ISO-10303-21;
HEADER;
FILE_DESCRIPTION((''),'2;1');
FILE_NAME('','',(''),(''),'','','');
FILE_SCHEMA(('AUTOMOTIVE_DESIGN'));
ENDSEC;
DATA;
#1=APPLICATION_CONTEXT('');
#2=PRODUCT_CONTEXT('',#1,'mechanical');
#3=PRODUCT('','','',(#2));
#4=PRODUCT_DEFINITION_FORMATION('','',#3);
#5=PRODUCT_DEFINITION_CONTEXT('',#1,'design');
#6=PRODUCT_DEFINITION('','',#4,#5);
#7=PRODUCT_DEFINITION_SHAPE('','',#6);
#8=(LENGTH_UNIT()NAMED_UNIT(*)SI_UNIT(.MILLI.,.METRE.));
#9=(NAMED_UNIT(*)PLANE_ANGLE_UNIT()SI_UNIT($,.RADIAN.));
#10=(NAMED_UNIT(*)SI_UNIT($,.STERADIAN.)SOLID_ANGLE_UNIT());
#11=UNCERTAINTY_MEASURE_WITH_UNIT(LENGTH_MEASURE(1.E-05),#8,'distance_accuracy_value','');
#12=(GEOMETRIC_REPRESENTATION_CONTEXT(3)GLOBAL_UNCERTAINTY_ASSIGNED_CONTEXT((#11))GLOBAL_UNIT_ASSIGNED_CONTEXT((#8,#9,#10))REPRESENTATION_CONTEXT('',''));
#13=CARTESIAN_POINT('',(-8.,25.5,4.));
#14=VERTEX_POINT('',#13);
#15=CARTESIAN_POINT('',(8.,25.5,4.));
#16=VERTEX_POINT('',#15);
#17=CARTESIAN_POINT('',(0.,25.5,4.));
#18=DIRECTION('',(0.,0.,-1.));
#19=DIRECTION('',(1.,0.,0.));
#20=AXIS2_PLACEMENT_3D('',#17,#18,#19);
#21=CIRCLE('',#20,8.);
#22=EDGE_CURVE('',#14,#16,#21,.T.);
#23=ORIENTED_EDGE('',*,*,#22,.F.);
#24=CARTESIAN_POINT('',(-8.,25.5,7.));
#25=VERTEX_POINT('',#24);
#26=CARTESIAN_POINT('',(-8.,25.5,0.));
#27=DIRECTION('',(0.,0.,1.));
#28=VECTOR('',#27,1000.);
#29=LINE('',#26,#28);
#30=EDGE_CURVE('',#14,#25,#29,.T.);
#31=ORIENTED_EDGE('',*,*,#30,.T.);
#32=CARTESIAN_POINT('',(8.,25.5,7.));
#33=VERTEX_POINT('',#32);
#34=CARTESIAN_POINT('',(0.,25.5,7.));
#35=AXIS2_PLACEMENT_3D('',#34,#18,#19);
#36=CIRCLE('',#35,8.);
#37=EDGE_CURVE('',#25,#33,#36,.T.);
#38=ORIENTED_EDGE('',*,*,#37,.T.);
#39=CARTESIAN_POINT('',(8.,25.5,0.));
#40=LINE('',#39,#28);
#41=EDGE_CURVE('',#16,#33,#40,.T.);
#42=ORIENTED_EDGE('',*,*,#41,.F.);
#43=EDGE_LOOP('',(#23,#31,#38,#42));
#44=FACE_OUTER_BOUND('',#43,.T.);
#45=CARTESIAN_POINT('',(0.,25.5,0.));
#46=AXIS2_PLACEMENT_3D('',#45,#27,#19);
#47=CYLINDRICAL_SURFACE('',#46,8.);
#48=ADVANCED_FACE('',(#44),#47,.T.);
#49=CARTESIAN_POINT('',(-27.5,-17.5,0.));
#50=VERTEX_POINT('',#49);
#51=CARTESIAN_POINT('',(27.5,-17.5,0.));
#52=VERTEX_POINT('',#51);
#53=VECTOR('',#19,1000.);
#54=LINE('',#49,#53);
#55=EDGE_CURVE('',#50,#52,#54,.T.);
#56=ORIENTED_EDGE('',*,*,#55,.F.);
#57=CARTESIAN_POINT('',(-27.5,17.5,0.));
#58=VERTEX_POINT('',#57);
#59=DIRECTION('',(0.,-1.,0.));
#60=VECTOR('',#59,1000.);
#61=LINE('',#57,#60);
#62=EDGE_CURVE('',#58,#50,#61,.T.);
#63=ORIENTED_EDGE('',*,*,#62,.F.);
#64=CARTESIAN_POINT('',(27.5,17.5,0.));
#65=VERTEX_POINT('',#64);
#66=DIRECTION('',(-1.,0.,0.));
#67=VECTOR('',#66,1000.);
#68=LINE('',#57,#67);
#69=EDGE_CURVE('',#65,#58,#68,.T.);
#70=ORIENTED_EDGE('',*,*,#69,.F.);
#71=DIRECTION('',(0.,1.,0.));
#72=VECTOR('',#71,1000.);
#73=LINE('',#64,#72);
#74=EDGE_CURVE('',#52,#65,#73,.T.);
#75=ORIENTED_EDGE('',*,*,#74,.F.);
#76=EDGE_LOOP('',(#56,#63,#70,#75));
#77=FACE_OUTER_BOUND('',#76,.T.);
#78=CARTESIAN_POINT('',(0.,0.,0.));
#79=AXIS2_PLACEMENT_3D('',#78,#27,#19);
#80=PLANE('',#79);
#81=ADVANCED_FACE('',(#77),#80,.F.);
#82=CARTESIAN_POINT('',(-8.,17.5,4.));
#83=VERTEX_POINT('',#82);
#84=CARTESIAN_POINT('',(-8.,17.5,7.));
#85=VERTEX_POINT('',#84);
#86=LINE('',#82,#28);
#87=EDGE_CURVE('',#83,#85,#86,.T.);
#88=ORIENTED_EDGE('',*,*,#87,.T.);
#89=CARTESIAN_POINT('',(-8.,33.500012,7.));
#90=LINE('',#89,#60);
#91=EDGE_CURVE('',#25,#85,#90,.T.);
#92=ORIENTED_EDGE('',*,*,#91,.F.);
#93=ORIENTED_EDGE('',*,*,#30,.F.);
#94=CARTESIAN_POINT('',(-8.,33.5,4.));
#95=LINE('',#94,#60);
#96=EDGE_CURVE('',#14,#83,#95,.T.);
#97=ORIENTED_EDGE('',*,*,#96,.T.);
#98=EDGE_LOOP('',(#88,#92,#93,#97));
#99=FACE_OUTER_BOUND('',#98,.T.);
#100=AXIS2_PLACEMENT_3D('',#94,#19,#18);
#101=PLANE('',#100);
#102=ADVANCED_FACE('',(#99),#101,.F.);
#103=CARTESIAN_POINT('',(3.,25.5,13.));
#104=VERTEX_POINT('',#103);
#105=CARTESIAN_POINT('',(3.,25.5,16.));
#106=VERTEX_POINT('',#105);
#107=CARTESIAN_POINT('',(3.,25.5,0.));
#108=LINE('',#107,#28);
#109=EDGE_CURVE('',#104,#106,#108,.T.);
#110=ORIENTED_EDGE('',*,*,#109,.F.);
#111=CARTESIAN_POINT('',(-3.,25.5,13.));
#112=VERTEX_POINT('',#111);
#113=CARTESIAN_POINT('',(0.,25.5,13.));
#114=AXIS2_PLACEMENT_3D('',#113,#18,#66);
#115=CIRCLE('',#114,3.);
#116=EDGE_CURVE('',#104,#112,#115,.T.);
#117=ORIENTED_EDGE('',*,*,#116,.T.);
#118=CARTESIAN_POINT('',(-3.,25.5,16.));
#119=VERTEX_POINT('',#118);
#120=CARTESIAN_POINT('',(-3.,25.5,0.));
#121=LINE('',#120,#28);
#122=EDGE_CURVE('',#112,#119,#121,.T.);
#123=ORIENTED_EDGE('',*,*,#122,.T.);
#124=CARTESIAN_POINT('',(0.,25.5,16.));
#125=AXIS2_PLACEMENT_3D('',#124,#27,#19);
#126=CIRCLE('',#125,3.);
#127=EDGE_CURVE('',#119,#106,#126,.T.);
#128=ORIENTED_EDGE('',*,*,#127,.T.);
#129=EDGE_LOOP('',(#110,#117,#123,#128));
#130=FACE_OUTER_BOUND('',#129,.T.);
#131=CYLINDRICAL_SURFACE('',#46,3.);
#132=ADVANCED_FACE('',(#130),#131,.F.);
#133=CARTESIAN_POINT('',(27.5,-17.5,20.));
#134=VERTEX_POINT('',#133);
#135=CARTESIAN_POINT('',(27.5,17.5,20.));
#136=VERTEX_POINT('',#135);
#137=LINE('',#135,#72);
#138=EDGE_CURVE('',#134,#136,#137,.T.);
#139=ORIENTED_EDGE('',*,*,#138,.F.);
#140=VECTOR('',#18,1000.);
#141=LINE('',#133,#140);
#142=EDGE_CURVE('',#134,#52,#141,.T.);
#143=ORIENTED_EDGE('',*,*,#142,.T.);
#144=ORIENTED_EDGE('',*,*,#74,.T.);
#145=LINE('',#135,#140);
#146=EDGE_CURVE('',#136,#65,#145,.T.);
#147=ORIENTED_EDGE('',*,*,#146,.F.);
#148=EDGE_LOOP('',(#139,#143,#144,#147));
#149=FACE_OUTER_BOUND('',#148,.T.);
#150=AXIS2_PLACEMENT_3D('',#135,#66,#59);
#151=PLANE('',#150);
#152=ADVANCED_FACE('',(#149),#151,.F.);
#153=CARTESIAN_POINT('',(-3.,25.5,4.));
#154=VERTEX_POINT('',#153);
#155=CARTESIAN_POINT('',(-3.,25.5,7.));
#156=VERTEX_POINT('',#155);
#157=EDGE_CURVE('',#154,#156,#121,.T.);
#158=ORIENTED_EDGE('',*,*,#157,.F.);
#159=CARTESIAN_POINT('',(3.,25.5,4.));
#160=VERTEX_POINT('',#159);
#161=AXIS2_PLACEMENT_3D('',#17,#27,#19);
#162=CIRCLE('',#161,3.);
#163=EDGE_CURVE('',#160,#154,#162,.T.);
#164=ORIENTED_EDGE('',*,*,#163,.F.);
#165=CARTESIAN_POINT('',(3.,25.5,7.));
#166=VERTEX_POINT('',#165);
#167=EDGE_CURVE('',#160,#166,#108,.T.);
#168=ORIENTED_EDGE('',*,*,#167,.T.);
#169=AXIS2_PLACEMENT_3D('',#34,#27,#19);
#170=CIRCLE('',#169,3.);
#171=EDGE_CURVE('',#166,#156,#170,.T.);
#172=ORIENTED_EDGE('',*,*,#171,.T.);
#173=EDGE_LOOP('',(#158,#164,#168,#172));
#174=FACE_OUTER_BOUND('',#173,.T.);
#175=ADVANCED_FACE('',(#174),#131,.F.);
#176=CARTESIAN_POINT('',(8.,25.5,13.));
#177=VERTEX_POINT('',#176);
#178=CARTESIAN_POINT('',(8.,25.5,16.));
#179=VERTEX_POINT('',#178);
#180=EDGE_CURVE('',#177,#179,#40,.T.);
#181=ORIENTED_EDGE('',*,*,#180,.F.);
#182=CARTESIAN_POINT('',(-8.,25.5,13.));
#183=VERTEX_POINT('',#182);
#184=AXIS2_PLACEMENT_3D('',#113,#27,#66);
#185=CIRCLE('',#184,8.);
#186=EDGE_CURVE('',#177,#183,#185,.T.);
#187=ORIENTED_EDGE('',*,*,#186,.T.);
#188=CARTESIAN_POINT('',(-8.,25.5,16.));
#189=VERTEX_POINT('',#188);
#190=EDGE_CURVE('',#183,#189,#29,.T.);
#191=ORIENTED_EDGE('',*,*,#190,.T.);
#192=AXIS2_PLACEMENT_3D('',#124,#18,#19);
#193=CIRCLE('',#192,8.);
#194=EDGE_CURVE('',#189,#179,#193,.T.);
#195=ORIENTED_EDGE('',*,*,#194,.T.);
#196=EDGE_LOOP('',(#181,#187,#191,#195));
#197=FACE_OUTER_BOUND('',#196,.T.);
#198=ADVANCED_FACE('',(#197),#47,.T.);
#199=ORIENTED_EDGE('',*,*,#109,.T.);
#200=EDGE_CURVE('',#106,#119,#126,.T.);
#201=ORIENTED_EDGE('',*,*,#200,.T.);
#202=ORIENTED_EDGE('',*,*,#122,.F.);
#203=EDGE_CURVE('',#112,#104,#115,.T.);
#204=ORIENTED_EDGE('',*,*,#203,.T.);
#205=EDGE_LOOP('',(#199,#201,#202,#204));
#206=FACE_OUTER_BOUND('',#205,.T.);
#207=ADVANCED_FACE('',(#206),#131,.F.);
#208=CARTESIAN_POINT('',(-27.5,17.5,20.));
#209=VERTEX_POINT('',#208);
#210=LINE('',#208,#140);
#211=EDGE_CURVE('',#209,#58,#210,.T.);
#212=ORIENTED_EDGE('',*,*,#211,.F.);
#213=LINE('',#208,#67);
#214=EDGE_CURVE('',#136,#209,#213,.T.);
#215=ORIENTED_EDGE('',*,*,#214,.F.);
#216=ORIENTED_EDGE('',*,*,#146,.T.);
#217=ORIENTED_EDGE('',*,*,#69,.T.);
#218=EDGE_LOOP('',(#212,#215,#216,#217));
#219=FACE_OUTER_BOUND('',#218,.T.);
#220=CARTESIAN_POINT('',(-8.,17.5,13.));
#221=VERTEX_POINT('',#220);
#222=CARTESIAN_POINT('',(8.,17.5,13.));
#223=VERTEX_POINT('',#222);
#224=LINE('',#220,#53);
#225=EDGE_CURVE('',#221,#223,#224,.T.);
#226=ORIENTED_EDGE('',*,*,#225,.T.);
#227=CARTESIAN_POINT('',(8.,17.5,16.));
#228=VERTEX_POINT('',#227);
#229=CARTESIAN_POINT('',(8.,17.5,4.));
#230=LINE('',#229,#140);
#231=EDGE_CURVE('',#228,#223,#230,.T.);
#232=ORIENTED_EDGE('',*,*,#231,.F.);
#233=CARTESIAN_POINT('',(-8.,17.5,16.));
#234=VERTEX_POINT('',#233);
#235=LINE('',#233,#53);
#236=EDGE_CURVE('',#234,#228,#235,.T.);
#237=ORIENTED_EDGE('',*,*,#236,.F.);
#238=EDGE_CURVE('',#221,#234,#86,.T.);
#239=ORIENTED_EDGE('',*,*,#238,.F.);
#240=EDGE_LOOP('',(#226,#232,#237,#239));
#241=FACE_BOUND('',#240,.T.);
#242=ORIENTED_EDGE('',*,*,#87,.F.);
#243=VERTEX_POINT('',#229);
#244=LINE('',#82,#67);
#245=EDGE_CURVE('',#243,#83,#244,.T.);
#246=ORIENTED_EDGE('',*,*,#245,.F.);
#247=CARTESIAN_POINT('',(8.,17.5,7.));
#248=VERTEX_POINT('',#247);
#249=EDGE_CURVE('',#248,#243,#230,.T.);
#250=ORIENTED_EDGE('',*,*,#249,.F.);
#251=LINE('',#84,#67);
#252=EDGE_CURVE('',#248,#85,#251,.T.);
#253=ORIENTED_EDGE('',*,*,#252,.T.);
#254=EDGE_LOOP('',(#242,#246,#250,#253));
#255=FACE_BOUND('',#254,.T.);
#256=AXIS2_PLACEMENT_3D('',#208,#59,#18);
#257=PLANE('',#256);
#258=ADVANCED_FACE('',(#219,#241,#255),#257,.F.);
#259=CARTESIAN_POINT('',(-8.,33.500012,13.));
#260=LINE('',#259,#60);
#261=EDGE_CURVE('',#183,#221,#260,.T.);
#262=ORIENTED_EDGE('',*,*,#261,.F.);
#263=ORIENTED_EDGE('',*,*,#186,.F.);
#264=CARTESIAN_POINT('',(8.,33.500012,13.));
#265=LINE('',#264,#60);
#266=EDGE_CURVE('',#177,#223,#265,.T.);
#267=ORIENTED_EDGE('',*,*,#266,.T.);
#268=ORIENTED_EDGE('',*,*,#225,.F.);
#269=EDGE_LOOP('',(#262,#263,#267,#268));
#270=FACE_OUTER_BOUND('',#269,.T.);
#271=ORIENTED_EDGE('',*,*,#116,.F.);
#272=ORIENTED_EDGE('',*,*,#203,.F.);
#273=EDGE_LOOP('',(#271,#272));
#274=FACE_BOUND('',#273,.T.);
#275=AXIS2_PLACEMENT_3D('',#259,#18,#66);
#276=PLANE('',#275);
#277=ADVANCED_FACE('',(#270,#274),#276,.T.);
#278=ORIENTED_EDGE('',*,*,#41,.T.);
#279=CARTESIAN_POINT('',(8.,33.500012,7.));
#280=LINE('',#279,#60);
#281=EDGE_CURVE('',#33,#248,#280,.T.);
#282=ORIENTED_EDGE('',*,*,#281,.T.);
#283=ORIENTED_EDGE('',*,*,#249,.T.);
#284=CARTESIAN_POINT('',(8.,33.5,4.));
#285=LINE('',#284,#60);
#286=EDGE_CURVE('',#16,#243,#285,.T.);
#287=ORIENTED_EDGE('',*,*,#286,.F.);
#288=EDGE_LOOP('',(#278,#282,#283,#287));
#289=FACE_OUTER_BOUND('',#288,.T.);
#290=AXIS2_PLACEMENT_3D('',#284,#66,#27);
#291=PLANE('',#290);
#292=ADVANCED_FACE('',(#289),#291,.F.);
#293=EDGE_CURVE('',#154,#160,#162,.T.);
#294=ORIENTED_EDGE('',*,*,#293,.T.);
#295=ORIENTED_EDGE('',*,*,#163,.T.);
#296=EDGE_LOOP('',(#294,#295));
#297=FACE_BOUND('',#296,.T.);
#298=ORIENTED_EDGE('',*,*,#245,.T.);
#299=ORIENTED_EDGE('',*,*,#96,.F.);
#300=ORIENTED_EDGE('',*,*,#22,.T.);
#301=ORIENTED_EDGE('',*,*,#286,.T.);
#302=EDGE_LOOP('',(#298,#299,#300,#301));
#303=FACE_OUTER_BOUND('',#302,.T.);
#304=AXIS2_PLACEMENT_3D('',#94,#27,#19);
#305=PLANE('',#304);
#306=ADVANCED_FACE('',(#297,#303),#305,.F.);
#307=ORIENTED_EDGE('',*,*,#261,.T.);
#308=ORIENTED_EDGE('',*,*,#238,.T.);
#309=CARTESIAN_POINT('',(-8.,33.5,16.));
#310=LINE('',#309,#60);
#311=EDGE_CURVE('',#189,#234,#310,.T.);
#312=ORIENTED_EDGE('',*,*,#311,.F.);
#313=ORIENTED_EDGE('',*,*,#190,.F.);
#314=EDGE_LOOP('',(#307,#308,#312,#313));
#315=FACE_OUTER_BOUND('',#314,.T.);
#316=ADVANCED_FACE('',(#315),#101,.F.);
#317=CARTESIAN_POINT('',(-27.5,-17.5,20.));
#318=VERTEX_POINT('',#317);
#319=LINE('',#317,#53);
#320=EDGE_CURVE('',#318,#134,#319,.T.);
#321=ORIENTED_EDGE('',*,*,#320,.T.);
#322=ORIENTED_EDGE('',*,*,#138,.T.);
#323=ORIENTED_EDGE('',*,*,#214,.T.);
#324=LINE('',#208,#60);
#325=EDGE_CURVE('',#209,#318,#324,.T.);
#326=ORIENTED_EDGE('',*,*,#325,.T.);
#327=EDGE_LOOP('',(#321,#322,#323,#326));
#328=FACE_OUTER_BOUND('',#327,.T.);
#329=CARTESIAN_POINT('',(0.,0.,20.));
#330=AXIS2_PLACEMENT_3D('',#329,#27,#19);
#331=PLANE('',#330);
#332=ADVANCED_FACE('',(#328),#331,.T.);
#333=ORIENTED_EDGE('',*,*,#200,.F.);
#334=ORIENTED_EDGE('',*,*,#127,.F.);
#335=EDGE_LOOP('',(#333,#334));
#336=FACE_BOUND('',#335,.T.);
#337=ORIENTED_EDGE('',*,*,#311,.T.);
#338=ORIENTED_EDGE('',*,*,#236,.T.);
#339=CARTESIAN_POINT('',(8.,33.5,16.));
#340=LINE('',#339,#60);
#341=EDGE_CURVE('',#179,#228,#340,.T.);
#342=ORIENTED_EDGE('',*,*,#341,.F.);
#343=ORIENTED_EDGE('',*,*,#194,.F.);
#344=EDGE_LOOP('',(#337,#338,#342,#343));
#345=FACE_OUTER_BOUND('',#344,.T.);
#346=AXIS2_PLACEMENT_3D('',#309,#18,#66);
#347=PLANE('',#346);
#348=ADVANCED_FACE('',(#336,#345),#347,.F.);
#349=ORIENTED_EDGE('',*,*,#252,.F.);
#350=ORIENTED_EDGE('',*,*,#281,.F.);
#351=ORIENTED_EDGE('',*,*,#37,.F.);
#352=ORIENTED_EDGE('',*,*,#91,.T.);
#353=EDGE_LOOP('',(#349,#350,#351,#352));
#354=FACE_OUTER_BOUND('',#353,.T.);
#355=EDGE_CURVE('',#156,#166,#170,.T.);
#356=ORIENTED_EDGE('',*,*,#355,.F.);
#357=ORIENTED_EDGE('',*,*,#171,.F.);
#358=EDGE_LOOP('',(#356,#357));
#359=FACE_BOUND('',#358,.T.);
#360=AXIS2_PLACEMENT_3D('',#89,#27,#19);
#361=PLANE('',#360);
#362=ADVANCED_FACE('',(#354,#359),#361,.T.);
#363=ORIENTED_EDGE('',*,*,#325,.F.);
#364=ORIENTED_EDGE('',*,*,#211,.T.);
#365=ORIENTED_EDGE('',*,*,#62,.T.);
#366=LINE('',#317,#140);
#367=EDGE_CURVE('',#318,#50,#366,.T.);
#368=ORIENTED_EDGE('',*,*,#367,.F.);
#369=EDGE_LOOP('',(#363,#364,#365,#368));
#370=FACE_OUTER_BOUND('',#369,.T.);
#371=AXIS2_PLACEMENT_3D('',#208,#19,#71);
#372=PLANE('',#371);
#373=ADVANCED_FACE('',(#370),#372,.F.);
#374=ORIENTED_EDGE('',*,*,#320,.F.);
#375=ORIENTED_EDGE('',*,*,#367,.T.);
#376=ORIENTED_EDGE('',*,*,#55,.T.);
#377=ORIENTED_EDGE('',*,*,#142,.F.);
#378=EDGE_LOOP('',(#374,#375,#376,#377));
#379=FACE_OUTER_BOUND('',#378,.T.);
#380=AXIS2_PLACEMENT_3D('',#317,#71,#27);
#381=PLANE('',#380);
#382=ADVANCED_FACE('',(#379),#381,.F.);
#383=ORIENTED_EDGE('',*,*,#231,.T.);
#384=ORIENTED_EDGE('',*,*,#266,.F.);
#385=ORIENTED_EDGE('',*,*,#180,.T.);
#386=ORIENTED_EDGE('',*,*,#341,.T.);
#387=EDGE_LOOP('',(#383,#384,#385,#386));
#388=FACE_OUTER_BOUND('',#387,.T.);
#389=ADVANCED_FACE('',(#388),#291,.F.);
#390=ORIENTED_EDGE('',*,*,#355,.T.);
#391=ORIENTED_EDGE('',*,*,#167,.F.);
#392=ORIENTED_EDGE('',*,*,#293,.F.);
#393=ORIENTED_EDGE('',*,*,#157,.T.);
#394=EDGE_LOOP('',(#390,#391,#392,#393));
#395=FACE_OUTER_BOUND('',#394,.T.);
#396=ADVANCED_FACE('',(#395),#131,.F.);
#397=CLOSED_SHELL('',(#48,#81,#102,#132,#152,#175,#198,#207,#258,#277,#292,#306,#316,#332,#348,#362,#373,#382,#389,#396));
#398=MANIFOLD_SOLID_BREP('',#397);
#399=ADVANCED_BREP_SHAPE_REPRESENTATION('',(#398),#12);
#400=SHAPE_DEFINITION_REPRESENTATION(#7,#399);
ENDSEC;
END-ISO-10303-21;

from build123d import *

# Parameters (mm, degrees)
SKETCH1_W               = 55
SKETCH1_H               = 35
BOSS_EXTRUDE1_DEPTH     = 20
SKETCH2_W               = 16
SKETCH2_H               = 12
BOSS_EXTRUDE2_DEPTH     = 16
CUT_EXTRUDE1_DEPTH      = 62.296410988
CUT_EXTRUDE1_DEPTH_BACK = 16
SKETCH3_W               = 16
SKETCH3_H               = 6
SKETCH4_R               = 3
CUT_EXTRUDE2_DEPTH      = 47.200649346


with BuildPart() as part:
    # Sketch1 → Boss-Extrude1 (new body)
    with BuildSketch(Plane.XY):
        Rectangle(SKETCH1_W, SKETCH1_H)
    extrude(amount=BOSS_EXTRUDE1_DEPTH)

    # Sketch2 → Boss-Extrude2 (add)
    with BuildSketch(Plane(origin=(0, 17.5, 0), x_dir=(1, 0, 0), z_dir=(0, 1, 0))):
        with Locations((0, -10)):
            Rectangle(SKETCH2_W, SKETCH2_H)
    extrude(amount=BOSS_EXTRUDE2_DEPTH)

    # Sketch3 → Cut-Extrude1 (cut, two sides: drawn at the far end of the back side and taken through both)
    with BuildSketch(Plane(origin=(0, 33.5, 0), x_dir=(1, 0, 0), z_dir=(0, 1, 0)).offset(-CUT_EXTRUDE1_DEPTH_BACK)):
        with Locations((0, -10)):
            Rectangle(SKETCH3_W, SKETCH3_H)
    extrude(amount=CUT_EXTRUDE1_DEPTH + CUT_EXTRUDE1_DEPTH_BACK, mode=Mode.SUBTRACT)

    # Sketch4 → Cut-Extrude2 (cut, through all)
    with BuildSketch(Plane.XY.offset(16)):
        with Locations((0, 25.5)):
            Circle(SKETCH4_R)
        with BuildLine():
            Line((-8, 25.5), (-21.64466881, 27.690296909))
            Line((-21.64466881, 27.690296909), (-8, 39.036178495))
            Line((-8, 39.036178495), (25.748849804, 31.989915092))
            Line((25.748849804, 31.989915092), (8, 25.5))
            ThreePointArc((8, 25.5), (0, 33.5), (-8, 25.5))
        make_face()
    extrude(amount=-CUT_EXTRUDE2_DEPTH, mode=Mode.SUBTRACT)


solid = part.part
